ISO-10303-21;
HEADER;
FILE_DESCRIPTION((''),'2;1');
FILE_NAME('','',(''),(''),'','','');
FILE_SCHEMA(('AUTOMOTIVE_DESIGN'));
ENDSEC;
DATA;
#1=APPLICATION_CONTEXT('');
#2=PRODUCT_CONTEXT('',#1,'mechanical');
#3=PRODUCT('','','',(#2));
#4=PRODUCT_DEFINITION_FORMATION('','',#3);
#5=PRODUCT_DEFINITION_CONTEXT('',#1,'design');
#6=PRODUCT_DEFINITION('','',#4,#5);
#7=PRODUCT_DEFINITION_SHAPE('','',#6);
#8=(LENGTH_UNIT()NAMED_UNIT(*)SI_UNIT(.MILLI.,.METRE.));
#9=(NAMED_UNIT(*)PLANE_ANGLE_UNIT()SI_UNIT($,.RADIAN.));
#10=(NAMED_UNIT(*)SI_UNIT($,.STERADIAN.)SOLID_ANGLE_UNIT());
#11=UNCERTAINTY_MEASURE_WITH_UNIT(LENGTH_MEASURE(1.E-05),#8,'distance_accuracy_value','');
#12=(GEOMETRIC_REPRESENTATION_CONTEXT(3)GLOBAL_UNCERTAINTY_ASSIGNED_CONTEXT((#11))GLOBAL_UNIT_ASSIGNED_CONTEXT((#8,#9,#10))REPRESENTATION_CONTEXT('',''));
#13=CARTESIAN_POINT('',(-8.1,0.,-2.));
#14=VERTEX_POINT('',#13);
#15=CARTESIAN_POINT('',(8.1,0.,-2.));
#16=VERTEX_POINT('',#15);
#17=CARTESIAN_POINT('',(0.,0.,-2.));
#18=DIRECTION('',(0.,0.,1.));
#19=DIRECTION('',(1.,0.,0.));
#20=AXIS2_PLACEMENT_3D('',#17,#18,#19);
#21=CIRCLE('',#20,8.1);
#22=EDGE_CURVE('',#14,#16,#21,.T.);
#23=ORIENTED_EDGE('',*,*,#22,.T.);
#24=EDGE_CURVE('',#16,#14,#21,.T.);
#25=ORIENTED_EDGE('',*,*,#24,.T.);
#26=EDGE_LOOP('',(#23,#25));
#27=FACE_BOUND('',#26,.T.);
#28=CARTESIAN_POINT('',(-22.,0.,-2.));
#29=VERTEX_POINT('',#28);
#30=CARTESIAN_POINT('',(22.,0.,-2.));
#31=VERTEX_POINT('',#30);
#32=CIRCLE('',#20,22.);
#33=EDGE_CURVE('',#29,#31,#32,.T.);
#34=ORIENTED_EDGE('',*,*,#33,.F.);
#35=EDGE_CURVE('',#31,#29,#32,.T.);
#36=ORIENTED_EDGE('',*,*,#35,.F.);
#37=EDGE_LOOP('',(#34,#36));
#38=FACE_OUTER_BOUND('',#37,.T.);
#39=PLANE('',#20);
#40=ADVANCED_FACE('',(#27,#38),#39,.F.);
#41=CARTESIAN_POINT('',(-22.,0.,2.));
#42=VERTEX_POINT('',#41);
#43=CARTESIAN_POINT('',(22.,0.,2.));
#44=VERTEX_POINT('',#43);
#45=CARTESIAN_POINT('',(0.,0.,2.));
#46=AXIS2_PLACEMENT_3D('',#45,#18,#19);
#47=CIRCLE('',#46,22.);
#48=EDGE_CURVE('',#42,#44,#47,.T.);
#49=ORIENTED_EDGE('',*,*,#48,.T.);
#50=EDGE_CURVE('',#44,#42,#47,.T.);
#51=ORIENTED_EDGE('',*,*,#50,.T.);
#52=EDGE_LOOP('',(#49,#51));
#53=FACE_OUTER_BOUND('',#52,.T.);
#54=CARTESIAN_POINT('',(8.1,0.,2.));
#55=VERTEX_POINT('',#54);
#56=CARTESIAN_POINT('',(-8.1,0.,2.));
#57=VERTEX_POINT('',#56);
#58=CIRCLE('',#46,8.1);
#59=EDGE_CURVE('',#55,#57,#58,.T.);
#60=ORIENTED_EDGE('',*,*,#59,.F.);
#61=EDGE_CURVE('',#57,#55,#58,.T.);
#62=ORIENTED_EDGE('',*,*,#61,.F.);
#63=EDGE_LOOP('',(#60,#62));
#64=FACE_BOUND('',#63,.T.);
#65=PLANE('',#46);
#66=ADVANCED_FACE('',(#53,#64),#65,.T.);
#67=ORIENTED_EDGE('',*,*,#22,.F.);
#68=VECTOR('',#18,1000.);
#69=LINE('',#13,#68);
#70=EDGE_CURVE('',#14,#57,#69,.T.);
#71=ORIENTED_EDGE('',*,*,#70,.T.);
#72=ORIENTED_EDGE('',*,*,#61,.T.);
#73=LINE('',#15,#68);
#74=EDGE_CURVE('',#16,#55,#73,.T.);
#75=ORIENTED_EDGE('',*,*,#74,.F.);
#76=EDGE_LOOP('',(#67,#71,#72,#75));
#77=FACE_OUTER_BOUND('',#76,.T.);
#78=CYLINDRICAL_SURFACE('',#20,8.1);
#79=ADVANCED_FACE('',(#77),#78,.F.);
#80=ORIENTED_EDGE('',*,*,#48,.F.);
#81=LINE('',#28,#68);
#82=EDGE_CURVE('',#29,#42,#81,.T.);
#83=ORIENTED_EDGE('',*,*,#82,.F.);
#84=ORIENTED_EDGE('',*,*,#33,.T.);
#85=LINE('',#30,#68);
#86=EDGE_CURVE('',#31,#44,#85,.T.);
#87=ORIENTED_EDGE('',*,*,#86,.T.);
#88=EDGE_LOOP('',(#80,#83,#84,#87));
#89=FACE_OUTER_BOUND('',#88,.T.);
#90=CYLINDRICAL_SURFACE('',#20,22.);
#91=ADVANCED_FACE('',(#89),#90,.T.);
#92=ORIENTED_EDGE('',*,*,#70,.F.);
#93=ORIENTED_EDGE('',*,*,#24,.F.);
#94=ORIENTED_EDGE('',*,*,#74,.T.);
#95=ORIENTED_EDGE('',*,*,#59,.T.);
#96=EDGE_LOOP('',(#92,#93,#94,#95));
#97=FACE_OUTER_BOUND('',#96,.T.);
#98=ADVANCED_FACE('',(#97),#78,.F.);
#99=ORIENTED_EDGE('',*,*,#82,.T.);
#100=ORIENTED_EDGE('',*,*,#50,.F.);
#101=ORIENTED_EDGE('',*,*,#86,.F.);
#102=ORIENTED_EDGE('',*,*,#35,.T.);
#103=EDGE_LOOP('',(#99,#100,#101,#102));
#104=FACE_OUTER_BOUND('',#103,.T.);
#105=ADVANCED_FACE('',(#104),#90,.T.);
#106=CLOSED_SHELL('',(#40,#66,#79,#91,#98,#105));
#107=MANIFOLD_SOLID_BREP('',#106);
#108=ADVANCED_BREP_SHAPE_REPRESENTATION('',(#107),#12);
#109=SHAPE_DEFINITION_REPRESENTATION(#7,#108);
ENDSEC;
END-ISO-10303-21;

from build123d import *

# Parameters (mm, degrees)
SKETCH_1_R      = 22
SKETCH_1_R_2    = 8.1
EXTRUDE_1_DEPTH = 2


with BuildPart() as part:
    # 草图1 → 凸台-拉伸1 (new, symmetric)
    with BuildSketch(Plane.XY):
        Circle(SKETCH_1_R)
        Circle(SKETCH_1_R_2, mode=Mode.SUBTRACT)
    extrude(amount=EXTRUDE_1_DEPTH, both=True)


solid = part.part
